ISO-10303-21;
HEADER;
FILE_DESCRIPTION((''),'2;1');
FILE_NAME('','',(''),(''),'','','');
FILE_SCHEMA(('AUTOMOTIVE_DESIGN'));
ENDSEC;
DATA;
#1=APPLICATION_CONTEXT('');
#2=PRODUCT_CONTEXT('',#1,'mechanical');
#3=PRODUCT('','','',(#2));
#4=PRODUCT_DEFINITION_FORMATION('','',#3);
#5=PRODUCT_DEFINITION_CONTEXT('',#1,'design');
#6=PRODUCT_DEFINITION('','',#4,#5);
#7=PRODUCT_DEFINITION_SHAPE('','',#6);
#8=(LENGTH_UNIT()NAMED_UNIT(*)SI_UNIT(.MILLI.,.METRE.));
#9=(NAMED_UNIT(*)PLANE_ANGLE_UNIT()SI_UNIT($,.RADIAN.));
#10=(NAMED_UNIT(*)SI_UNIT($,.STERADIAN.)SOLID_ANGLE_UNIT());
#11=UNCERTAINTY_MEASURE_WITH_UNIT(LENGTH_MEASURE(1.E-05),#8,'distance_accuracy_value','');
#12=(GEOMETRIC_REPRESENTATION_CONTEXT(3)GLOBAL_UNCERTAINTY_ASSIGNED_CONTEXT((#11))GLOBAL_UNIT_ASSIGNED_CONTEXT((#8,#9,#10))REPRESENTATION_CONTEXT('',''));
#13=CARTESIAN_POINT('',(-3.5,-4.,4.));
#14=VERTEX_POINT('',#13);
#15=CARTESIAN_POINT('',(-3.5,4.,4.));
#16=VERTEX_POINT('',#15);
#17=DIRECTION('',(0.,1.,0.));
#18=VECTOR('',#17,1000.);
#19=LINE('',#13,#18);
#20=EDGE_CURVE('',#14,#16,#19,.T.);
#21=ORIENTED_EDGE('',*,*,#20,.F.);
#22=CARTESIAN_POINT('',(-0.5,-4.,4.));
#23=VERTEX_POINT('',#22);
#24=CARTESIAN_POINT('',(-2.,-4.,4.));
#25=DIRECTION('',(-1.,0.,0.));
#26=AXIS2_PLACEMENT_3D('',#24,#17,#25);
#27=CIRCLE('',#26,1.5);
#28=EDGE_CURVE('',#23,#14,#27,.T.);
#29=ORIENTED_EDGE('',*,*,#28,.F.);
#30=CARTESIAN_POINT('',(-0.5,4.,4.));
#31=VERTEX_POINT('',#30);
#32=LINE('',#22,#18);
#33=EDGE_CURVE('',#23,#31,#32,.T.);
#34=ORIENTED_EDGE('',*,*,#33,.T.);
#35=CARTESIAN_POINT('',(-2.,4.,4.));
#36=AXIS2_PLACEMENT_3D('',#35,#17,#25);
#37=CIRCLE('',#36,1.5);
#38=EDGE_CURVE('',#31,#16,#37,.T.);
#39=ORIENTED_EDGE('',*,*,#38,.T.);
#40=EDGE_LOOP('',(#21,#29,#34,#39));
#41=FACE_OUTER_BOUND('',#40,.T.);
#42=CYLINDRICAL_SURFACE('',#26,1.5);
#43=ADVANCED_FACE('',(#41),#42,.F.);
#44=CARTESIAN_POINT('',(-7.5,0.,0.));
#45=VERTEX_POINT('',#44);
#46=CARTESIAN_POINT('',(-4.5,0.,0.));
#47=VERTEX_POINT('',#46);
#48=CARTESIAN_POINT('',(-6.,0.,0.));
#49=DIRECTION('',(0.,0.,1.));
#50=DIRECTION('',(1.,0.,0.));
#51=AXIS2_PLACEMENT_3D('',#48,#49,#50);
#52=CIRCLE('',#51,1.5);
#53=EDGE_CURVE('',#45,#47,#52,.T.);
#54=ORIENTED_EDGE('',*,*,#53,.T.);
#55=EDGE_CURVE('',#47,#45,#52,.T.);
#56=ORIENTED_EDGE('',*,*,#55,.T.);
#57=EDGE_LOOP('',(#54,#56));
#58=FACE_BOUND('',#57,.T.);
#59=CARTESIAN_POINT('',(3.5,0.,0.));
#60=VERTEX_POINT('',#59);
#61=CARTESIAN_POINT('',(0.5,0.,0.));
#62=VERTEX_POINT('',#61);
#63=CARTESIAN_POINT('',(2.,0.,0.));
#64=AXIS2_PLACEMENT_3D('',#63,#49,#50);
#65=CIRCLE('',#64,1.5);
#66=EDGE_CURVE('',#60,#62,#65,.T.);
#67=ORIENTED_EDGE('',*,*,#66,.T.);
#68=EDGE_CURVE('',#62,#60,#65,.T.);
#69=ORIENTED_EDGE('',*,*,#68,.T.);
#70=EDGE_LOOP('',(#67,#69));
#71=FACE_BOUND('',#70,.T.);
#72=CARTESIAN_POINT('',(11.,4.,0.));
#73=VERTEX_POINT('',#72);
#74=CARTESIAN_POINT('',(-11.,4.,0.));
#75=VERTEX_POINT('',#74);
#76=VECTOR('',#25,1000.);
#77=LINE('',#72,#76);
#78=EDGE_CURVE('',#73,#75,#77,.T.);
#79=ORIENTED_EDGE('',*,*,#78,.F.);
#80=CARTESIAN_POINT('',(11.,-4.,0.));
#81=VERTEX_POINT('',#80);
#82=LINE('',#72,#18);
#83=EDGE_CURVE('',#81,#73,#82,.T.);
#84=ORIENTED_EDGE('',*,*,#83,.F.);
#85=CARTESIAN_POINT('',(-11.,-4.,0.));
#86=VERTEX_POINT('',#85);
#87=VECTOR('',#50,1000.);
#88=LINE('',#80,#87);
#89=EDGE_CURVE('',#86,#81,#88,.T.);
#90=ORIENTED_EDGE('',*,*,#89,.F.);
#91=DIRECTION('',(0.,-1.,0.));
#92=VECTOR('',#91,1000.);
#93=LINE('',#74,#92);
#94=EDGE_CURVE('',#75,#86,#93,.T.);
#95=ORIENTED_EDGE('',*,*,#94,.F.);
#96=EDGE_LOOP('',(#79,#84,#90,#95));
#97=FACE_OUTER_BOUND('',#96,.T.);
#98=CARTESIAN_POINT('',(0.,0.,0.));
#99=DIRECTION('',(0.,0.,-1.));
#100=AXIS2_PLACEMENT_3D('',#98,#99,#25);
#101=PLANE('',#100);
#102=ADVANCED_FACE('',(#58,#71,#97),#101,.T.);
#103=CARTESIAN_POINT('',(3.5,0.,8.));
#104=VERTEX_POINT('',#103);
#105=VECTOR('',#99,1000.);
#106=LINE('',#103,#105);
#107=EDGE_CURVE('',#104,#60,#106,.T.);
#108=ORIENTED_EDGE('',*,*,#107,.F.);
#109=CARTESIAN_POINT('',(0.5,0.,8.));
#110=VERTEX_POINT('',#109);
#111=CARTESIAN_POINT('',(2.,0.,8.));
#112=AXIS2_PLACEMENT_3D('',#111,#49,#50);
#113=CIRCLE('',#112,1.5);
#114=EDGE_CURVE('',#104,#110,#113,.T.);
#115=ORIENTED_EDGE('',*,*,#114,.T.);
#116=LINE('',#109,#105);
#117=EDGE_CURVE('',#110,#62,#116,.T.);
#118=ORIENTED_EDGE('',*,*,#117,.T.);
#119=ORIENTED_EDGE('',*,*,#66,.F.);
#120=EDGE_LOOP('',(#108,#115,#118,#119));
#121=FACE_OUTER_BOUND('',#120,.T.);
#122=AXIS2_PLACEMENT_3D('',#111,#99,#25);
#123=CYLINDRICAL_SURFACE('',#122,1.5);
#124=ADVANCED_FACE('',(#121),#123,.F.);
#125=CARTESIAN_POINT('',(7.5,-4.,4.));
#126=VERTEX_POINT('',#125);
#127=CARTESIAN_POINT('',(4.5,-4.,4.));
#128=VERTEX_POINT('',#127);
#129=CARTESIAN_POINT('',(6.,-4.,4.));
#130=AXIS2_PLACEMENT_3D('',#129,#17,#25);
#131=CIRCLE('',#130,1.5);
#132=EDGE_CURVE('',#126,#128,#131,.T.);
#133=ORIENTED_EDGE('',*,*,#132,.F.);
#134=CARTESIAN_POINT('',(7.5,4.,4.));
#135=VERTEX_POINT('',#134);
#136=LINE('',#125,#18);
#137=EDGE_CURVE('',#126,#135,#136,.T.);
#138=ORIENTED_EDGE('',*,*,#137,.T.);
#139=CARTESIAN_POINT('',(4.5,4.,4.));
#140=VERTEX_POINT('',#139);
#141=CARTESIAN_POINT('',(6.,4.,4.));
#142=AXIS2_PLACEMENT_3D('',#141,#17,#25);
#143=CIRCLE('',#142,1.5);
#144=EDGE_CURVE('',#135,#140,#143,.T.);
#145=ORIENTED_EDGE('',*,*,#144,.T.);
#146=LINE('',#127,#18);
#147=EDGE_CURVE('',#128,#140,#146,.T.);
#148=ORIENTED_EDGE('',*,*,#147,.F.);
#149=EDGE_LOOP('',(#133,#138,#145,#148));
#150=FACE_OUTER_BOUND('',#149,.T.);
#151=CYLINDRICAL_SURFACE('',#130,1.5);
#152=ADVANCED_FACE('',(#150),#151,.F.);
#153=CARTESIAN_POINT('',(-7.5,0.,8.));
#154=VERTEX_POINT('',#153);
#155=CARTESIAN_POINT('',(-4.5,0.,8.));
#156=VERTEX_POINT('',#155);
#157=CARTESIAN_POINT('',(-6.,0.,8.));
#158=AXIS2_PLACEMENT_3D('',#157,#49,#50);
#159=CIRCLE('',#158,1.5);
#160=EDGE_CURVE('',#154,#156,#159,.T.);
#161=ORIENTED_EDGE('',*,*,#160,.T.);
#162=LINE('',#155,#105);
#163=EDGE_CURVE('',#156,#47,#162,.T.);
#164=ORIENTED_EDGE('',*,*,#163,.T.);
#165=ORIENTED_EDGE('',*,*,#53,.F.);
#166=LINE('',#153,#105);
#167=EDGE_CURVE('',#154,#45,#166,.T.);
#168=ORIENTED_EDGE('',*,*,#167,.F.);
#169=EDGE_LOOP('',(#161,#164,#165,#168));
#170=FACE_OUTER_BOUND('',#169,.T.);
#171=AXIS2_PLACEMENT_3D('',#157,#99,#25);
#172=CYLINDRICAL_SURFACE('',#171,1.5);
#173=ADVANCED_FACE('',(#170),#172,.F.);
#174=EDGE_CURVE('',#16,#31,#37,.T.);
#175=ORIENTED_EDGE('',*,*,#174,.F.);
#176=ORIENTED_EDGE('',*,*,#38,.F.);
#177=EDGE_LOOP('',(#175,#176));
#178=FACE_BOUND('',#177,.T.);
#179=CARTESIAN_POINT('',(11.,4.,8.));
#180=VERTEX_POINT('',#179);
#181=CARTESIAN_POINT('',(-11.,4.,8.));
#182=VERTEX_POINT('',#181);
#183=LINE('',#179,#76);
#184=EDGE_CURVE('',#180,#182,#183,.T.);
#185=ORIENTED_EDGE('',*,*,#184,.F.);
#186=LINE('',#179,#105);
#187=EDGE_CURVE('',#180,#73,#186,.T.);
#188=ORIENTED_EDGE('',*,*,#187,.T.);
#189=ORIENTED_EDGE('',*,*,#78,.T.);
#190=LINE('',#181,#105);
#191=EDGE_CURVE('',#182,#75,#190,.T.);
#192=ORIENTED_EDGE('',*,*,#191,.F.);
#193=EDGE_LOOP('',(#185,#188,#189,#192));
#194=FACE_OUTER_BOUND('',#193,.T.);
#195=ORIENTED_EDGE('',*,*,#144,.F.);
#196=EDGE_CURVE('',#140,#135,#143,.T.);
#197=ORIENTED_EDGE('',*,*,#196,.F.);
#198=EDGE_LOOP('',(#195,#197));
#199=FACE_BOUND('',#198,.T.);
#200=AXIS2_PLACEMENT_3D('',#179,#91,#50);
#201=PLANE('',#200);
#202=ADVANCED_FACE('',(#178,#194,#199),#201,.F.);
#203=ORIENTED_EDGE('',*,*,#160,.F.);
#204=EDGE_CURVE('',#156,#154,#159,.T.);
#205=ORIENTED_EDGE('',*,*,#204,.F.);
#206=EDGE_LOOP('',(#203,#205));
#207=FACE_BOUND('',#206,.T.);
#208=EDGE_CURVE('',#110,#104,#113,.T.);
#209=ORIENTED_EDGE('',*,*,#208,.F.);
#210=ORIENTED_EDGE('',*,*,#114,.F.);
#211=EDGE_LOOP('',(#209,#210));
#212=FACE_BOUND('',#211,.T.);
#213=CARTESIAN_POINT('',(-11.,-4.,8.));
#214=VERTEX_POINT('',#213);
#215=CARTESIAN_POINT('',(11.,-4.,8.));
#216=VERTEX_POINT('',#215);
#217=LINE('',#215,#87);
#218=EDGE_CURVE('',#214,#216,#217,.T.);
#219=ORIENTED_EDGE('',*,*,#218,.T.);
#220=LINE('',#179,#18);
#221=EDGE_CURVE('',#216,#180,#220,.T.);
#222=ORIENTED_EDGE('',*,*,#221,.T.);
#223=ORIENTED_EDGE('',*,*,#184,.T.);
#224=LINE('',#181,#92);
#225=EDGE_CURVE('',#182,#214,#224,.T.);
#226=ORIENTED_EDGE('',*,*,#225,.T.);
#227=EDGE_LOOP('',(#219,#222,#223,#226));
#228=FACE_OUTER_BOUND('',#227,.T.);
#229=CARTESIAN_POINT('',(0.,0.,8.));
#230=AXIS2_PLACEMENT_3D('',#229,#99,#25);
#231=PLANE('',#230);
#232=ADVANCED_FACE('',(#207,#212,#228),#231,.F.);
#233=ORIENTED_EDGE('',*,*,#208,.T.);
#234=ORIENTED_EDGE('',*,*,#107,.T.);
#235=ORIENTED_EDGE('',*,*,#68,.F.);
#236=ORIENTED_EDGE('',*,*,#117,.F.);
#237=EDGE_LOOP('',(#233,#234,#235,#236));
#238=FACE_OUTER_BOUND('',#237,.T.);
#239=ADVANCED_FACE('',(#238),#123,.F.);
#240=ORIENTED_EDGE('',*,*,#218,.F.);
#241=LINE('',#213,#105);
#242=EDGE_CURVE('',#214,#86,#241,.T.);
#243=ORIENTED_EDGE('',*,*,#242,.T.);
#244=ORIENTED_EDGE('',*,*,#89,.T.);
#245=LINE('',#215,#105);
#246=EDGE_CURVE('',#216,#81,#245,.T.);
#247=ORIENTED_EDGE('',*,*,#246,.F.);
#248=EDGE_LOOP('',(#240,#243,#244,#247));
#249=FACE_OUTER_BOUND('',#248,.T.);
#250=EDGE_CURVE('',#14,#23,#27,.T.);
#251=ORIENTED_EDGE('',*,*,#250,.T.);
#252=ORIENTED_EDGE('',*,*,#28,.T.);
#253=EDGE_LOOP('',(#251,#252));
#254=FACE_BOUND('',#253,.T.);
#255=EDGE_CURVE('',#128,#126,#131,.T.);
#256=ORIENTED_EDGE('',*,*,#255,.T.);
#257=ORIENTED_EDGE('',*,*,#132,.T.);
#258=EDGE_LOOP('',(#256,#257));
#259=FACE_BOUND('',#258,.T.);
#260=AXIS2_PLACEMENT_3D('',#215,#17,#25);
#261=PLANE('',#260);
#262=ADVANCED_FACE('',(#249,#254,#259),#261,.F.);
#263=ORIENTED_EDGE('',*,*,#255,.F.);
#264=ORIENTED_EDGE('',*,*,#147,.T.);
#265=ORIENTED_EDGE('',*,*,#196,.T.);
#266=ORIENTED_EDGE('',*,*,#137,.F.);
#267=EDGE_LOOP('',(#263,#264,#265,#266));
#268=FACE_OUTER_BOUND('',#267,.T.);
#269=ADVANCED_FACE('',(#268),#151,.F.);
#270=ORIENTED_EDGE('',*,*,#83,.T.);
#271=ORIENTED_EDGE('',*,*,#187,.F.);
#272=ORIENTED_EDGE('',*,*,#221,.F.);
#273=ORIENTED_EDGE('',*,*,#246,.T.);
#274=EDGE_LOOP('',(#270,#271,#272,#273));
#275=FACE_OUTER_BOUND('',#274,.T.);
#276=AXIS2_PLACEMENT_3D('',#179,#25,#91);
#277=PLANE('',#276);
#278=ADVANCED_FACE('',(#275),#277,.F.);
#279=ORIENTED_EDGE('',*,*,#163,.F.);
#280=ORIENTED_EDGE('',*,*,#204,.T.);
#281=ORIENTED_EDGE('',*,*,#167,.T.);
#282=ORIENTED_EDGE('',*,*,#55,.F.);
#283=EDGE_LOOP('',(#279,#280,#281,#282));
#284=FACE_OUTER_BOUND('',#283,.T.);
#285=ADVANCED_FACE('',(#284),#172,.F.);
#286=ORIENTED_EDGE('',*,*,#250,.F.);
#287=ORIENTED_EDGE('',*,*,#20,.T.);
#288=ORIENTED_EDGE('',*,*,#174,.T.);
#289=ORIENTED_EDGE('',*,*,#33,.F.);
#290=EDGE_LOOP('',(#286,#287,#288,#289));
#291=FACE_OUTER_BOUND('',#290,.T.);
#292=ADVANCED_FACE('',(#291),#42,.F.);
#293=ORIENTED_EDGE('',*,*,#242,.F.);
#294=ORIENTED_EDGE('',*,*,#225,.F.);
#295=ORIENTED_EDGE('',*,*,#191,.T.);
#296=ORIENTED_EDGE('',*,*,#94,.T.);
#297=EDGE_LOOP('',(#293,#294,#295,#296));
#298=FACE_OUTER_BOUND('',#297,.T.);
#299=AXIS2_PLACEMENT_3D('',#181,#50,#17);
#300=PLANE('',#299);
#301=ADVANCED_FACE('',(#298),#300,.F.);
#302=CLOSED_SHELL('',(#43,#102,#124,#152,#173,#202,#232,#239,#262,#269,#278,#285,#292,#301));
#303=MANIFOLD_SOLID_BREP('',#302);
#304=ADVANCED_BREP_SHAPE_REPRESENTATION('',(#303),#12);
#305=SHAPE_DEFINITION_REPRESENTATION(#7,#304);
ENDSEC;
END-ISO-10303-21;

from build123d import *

# Parameters (mm, degrees)
SKETCH_1_W          = 22
SKETCH_1_H          = 8
SKETCH_1_R          = 1.5
EXTRUDE_1_DEPTH     = 8
SKETCH_2_R          = 1.5
CUT_EXTRUDE_1_DEPTH = 16.779733838


with BuildPart() as part:
    # 草图1 → 凸台-拉伸1 (new body)
    with BuildSketch(Plane.XY):
        Rectangle(SKETCH_1_W, SKETCH_1_H)
        with Locations((-6, 0)):
            Circle(SKETCH_1_R, mode=Mode.SUBTRACT)
        with Locations((2, 0)):
            Circle(SKETCH_1_R, mode=Mode.SUBTRACT)
    extrude(amount=EXTRUDE_1_DEPTH)

    # 草图2 → 切除-拉伸1 (cut, through all)
    with BuildSketch(Plane(origin=(0, 4, 0), x_dir=(1, 0, 0), z_dir=(0, 1, 0))):
        with Locations(Location((6, -4, 0), (0, 0, 180))):
            Circle(SKETCH_2_R)
        with Locations(Location((-2, -4, 0), (0, 0, 180))):
            Circle(SKETCH_2_R)
    extrude(amount=-CUT_EXTRUDE_1_DEPTH, mode=Mode.SUBTRACT)


solid = part.part
